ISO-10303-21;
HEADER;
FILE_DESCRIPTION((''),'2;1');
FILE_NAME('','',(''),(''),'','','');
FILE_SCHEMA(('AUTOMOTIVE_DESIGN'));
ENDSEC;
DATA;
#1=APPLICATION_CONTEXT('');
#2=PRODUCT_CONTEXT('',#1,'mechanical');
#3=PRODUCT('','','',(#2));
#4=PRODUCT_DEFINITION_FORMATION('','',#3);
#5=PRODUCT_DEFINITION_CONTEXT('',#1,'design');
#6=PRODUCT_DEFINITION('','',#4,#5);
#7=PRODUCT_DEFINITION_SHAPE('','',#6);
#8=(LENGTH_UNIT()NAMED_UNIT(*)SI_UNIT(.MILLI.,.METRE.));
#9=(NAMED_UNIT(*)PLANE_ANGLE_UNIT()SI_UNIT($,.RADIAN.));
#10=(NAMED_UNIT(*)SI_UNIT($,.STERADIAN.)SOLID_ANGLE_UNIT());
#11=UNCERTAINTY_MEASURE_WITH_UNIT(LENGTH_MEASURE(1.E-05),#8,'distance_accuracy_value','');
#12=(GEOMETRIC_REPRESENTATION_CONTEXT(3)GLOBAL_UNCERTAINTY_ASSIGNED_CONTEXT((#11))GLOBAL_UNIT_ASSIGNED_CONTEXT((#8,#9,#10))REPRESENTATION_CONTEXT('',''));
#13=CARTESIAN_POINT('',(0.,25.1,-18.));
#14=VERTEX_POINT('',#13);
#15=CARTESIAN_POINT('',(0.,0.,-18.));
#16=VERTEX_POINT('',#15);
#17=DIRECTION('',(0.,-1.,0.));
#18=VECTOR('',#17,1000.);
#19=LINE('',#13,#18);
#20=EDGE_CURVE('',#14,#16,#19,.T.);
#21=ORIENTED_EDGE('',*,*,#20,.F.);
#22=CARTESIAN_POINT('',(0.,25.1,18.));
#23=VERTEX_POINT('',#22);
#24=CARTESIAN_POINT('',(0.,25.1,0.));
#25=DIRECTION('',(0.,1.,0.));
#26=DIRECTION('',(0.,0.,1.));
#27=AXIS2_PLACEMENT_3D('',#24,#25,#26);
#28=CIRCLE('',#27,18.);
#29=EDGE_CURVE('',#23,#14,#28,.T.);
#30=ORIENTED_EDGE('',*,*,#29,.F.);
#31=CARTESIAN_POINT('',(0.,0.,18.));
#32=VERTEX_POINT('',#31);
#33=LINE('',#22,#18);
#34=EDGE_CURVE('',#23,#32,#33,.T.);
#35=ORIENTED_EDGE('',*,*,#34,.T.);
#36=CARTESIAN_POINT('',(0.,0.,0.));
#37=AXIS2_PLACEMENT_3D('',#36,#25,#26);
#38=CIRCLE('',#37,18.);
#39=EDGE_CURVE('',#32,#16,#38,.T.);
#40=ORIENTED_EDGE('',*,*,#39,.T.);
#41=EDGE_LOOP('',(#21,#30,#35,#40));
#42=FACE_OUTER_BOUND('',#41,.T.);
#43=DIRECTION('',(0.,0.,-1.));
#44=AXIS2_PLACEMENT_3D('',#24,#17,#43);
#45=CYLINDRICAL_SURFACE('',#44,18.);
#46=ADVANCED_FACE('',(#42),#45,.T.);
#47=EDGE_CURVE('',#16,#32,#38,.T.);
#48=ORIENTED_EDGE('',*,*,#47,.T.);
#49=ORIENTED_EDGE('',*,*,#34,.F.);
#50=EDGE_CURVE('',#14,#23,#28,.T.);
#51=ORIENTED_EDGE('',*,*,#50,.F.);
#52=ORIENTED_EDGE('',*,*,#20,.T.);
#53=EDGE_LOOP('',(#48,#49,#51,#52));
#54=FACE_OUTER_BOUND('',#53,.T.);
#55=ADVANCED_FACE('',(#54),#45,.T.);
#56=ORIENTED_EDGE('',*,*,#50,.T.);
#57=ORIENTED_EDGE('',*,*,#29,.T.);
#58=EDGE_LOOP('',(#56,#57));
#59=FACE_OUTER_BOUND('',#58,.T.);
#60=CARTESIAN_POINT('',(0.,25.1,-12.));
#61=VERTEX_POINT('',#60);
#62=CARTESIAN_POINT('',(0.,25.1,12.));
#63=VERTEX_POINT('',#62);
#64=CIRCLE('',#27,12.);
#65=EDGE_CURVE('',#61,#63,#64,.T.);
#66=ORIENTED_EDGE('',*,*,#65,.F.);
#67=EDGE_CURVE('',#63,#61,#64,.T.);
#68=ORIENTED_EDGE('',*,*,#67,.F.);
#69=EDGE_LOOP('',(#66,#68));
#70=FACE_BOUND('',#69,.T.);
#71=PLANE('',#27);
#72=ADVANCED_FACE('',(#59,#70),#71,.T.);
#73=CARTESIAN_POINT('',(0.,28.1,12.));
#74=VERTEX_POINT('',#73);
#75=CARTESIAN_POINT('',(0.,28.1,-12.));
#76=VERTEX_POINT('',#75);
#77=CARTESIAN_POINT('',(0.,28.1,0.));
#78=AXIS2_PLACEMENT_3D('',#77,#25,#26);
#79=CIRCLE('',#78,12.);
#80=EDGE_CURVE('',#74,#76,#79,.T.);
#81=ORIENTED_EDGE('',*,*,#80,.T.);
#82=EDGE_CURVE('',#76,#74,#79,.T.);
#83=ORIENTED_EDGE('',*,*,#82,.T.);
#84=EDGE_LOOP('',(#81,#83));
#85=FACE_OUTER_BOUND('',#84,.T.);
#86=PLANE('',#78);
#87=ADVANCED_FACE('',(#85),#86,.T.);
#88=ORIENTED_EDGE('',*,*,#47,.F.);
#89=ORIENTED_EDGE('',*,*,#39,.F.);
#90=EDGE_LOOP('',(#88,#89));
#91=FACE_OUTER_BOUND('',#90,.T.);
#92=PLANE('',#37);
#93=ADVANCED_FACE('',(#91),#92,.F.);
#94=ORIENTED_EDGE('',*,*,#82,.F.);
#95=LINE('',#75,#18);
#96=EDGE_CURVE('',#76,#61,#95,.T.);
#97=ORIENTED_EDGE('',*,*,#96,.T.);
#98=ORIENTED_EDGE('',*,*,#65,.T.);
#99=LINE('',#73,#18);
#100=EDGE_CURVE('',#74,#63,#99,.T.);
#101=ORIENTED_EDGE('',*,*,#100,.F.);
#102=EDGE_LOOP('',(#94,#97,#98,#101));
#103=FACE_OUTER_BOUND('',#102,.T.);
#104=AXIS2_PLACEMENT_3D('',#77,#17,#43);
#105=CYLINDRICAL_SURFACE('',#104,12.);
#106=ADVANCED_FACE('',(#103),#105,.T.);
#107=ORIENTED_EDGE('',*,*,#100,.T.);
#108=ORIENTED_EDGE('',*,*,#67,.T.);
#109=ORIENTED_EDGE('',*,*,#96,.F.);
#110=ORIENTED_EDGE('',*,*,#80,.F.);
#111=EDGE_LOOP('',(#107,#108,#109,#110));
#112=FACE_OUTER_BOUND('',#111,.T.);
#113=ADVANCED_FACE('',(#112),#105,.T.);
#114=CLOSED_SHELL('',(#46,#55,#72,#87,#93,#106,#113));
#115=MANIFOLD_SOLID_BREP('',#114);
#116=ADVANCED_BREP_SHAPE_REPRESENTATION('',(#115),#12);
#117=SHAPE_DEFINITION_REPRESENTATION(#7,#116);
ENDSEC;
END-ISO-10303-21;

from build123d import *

# Parameters (mm, degrees)
SKETCH_1_R      = 18
EXTRUDE_1_DEPTH = 25.1
SKETCH_2_R      = 12
EXTRUDE_2_DEPTH = 3


with BuildPart() as part:
    # 草图1 → 凸台-拉伸1 (new body)
    with BuildSketch(Plane(origin=(0, 0, 0), x_dir=(1, 0, 0), z_dir=(0, 1, 0))):
        with Locations(Location((0, 0, 0), (0, 0, 270))):
            Circle(SKETCH_1_R)
    extrude(amount=EXTRUDE_1_DEPTH)

    # 草图2 → 凸台-拉伸2 (add)
    with BuildSketch(Plane(origin=(0, 25.1, 0), x_dir=(1, 0, 0), z_dir=(0, 1, 0))):
        with Locations(Location((0, 0, 0), (0, 0, 270))):
            Circle(SKETCH_2_R)
    extrude(amount=EXTRUDE_2_DEPTH)


solid = part.part
